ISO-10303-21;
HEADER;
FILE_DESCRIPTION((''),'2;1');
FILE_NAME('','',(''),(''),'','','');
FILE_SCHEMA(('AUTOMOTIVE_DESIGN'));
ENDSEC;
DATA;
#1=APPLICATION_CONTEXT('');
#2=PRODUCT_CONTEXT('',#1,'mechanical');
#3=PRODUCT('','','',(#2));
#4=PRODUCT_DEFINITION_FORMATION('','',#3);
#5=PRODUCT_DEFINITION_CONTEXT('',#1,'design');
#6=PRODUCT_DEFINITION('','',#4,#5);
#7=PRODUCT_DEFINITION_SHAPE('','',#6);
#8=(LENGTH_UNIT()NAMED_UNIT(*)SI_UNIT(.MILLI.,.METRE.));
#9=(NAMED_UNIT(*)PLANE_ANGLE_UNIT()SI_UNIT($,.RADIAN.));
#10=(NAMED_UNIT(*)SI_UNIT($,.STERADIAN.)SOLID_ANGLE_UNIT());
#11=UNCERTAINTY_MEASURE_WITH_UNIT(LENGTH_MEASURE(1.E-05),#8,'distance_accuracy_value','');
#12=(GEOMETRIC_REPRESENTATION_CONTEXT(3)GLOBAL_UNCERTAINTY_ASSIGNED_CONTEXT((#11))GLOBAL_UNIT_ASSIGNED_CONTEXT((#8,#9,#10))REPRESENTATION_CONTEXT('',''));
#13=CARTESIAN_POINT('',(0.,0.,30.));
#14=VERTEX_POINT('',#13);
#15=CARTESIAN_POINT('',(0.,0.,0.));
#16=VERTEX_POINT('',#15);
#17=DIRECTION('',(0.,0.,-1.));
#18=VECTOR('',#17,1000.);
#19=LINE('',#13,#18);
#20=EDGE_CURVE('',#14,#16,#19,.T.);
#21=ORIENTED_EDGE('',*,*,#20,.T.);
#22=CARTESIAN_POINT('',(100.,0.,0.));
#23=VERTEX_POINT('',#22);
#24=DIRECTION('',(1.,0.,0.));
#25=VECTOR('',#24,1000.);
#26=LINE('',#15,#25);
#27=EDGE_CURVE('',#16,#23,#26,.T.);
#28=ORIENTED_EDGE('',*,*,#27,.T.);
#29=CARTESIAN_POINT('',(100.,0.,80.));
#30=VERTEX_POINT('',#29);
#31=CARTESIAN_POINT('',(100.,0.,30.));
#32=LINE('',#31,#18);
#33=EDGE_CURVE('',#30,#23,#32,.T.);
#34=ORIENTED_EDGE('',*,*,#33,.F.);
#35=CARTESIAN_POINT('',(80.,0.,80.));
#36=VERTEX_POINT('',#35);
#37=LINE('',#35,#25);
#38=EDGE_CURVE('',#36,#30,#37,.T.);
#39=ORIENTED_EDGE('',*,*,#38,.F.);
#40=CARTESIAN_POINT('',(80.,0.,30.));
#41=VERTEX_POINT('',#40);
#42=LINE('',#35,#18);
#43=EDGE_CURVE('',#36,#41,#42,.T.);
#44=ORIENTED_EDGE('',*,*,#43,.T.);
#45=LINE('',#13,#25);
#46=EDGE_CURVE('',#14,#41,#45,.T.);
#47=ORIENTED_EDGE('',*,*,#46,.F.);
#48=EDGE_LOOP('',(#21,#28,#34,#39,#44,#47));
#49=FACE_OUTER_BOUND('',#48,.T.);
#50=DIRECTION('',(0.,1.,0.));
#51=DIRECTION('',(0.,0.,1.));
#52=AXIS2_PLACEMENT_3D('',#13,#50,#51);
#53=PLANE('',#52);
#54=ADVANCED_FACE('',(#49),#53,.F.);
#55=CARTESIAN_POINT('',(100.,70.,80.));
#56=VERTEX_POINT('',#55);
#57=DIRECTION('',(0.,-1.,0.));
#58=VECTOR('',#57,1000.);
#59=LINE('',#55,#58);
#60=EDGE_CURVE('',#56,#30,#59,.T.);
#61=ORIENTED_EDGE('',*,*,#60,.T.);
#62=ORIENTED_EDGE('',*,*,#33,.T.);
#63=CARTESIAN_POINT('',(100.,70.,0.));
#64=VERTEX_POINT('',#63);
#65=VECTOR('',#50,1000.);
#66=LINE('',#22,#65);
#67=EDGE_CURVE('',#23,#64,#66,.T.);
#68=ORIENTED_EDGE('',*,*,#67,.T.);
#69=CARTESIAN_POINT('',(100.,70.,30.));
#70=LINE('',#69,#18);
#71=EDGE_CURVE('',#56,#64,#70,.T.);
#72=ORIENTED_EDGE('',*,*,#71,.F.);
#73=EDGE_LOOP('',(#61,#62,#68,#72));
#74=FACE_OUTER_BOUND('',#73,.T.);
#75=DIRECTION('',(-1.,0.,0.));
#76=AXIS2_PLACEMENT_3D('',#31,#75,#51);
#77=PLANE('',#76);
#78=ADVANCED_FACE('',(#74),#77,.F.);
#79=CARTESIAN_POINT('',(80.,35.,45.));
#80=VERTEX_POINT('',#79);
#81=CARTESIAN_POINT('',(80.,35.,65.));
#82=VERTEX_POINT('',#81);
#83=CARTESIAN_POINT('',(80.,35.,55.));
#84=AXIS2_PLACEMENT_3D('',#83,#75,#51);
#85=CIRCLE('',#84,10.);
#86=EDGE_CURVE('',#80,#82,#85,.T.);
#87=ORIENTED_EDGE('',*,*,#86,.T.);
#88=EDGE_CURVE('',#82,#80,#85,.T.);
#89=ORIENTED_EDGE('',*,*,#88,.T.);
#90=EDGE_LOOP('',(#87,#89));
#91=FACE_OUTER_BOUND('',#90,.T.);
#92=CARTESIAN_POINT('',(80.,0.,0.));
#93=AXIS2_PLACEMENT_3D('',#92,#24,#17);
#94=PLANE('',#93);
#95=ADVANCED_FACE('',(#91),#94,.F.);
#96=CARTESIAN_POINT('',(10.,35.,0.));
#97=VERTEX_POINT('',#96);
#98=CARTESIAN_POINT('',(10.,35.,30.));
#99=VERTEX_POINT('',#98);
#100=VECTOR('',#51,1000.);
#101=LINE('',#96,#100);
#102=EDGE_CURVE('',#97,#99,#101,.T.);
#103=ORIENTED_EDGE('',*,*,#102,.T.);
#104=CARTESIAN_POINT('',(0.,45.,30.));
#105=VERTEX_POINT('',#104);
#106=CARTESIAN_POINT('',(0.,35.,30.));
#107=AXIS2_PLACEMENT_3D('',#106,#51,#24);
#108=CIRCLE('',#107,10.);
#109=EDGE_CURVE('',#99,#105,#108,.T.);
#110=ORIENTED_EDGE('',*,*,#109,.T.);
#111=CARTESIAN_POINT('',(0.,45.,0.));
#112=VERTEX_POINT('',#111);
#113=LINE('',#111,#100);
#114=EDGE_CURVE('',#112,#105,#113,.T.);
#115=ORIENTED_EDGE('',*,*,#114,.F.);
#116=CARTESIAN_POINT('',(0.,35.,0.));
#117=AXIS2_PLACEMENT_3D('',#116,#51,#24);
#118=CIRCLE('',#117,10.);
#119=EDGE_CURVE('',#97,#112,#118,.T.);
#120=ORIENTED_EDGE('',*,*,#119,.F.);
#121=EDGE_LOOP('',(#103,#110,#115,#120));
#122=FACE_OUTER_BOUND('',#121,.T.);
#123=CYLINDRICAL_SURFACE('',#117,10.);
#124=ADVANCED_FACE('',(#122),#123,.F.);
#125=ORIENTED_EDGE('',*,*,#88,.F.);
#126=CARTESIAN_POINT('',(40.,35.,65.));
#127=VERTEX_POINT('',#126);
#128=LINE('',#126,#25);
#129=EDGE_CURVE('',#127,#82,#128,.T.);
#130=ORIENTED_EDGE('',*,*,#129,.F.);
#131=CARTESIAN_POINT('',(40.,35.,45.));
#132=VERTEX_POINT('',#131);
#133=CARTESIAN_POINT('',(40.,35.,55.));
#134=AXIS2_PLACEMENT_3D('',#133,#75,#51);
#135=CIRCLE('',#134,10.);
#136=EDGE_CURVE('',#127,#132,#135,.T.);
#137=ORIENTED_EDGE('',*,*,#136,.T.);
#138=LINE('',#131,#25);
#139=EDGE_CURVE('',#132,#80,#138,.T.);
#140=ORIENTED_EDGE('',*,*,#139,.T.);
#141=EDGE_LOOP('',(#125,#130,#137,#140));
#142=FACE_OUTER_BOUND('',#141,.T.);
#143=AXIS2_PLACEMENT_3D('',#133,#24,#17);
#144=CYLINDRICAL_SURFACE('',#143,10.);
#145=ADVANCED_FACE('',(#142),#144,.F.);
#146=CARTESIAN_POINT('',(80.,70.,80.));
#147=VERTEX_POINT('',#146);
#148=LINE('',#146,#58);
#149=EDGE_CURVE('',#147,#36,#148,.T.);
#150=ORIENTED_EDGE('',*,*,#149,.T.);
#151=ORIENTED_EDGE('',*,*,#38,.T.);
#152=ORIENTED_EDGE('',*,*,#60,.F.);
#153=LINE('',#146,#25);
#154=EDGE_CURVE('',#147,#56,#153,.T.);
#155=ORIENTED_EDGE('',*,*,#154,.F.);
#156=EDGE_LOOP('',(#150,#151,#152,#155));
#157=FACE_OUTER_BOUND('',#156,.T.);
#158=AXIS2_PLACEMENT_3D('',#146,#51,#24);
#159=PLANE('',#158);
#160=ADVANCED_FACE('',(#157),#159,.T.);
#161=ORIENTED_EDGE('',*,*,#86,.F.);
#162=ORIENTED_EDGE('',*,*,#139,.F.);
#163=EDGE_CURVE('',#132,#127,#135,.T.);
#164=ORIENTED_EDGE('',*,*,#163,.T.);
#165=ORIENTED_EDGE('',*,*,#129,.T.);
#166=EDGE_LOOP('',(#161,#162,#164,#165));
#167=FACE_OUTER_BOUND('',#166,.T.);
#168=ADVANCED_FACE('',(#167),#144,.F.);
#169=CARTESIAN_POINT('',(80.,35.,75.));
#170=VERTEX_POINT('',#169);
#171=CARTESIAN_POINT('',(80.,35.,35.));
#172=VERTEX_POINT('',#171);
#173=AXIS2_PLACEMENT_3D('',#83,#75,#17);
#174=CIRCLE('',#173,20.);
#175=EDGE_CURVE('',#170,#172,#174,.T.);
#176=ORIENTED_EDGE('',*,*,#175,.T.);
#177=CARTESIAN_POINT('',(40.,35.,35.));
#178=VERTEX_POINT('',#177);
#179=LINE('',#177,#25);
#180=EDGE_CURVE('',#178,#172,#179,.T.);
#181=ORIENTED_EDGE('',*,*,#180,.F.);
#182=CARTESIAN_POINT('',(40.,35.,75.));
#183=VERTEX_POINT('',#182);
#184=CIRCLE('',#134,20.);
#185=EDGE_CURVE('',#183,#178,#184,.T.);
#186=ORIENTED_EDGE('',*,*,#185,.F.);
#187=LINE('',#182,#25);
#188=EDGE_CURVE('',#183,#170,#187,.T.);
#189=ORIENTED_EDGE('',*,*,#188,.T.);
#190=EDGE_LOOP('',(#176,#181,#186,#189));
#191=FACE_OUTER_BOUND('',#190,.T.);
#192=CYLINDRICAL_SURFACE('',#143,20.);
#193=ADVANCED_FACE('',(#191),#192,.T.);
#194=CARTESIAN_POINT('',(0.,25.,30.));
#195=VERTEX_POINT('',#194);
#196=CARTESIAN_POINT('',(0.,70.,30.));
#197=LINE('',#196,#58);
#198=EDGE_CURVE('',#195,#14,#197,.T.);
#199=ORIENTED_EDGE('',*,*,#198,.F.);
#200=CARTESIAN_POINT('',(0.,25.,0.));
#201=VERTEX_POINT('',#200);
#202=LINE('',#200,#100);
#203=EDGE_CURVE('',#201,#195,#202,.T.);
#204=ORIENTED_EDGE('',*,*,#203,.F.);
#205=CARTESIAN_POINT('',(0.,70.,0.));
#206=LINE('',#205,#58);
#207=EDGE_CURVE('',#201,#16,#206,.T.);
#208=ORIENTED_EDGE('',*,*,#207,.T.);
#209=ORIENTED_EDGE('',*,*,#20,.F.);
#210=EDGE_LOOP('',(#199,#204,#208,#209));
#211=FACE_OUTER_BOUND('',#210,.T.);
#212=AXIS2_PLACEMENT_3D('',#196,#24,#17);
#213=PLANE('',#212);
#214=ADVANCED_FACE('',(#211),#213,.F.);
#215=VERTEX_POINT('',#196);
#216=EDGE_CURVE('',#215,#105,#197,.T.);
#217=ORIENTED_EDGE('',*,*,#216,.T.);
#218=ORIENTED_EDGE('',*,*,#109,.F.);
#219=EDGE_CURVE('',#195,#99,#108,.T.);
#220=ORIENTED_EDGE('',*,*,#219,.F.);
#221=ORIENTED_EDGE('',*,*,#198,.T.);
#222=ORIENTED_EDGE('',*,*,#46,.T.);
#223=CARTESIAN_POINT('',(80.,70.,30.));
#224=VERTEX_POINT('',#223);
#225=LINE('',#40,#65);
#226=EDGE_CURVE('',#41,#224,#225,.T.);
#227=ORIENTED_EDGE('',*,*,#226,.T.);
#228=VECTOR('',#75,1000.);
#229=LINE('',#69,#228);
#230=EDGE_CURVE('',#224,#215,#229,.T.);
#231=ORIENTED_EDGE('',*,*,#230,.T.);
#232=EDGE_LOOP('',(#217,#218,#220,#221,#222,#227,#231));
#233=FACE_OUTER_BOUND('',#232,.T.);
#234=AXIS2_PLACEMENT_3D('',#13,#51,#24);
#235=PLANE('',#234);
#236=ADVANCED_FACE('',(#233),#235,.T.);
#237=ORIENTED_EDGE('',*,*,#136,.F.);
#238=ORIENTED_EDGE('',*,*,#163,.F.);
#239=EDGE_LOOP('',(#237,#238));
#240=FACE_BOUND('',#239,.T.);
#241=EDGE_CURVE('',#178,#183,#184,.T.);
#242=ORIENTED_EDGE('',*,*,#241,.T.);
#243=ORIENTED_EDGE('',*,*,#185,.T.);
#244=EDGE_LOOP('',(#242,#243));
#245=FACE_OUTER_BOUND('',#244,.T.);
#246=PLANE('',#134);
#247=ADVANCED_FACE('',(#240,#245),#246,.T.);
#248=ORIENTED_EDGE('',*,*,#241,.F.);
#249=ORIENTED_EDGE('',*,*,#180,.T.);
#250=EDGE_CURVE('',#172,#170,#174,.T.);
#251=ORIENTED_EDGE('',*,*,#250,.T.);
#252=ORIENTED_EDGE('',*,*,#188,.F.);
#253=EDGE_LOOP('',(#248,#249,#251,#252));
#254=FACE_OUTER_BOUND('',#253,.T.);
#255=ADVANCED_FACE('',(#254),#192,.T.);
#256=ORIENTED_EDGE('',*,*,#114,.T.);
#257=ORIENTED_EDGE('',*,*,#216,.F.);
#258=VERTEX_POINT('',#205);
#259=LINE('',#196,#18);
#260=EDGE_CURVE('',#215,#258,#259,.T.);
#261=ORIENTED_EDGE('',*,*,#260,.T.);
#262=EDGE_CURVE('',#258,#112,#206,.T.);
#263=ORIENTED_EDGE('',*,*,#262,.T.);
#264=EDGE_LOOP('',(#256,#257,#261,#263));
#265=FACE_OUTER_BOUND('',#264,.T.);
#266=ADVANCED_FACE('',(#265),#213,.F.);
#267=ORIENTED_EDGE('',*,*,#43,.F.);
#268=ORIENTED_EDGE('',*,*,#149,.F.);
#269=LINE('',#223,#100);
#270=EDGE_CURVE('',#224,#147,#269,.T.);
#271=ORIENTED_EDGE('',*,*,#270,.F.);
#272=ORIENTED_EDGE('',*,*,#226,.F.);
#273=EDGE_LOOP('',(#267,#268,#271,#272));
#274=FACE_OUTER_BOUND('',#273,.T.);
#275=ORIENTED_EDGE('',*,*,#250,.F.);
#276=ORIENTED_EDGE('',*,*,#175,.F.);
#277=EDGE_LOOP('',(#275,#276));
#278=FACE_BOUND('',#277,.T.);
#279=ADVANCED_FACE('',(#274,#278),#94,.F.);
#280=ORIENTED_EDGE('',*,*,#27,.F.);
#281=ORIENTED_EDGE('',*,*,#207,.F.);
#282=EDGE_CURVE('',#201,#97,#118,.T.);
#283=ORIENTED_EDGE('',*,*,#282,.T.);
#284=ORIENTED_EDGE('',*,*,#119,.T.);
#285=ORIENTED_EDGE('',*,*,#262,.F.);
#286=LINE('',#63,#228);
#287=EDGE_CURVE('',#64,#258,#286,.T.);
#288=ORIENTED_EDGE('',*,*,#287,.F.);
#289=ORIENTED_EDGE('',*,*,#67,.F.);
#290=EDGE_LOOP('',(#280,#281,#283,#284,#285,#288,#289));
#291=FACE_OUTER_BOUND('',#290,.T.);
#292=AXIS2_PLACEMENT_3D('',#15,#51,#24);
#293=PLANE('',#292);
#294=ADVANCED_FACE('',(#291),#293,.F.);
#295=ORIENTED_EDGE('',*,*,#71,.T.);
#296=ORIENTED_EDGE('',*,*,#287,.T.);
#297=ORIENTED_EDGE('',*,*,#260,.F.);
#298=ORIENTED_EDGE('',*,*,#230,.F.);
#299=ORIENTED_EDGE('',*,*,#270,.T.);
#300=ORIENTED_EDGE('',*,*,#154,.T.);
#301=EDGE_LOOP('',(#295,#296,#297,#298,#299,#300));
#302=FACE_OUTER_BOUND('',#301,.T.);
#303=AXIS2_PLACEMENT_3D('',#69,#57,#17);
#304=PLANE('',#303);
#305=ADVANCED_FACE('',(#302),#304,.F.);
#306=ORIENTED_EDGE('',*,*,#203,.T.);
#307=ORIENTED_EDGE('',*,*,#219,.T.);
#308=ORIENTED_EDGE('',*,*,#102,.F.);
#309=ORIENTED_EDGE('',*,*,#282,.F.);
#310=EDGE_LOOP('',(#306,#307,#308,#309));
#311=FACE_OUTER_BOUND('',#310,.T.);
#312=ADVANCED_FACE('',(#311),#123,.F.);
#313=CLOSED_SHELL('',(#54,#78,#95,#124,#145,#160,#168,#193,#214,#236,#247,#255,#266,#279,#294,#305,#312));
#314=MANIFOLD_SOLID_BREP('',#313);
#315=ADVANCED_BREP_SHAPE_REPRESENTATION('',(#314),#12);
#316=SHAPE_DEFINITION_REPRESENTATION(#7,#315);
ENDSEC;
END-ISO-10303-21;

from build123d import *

# Parameters (mm, degrees)
BASE_PLATE_SKETCH_W        = 100
BASE_PLATE_SKETCH_H        = 70
BASE_PLATE_DEPTH           = 30
SEMICIRCULAR_NOTCH_DEPTH   = 30
UPRIGHT_WALL_SKETCH_W      = 50
UPRIGHT_WALL_SKETCH_H      = 70
UPRIGHT_WALL_DEPTH         = 20
HALF_ROUND_BOSS_SKETCH_R   = 20
HALF_ROUND_BOSS_SKETCH_R_2 = 10
HALF_ROUND_BOSS_DEPTH      = 40


with BuildPart() as part:
    # Base Plate Sketch → Base Plate (new body)
    with BuildSketch(Plane.XY):
        with Locations((50, 35)):
            Rectangle(BASE_PLATE_SKETCH_W, BASE_PLATE_SKETCH_H)
    extrude(amount=BASE_PLATE_DEPTH)

    # Notch Sketch → Semicircular Notch (cut)
    with BuildSketch(Plane.XY.offset(30)):
        with BuildLine():
            Line((0, 45), (0, 25))
            ThreePointArc((0, 25), (10, 35), (0, 45))
        make_face()
    extrude(amount=-SEMICIRCULAR_NOTCH_DEPTH, mode=Mode.SUBTRACT)

    # Upright Wall Sketch → Upright Wall (add)
    with BuildSketch(Plane(origin=(100, 0, 0), x_dir=(0, 0, -1), z_dir=(1, 0, 0))):
        with Locations((-55, 35)):
            Rectangle(UPRIGHT_WALL_SKETCH_W, UPRIGHT_WALL_SKETCH_H)
    extrude(amount=-UPRIGHT_WALL_DEPTH)

    # Half-Round Boss Sketch → Half-Round Boss (add)
    with BuildSketch(Plane.ZY.offset(-80)):
        with Locations(Location((55, 35, 0), (0, 0, 180))):
            Circle(HALF_ROUND_BOSS_SKETCH_R)
        with Locations((55, 35)):
            Circle(HALF_ROUND_BOSS_SKETCH_R_2, mode=Mode.SUBTRACT)
    extrude(amount=HALF_ROUND_BOSS_DEPTH)


solid = part.part
